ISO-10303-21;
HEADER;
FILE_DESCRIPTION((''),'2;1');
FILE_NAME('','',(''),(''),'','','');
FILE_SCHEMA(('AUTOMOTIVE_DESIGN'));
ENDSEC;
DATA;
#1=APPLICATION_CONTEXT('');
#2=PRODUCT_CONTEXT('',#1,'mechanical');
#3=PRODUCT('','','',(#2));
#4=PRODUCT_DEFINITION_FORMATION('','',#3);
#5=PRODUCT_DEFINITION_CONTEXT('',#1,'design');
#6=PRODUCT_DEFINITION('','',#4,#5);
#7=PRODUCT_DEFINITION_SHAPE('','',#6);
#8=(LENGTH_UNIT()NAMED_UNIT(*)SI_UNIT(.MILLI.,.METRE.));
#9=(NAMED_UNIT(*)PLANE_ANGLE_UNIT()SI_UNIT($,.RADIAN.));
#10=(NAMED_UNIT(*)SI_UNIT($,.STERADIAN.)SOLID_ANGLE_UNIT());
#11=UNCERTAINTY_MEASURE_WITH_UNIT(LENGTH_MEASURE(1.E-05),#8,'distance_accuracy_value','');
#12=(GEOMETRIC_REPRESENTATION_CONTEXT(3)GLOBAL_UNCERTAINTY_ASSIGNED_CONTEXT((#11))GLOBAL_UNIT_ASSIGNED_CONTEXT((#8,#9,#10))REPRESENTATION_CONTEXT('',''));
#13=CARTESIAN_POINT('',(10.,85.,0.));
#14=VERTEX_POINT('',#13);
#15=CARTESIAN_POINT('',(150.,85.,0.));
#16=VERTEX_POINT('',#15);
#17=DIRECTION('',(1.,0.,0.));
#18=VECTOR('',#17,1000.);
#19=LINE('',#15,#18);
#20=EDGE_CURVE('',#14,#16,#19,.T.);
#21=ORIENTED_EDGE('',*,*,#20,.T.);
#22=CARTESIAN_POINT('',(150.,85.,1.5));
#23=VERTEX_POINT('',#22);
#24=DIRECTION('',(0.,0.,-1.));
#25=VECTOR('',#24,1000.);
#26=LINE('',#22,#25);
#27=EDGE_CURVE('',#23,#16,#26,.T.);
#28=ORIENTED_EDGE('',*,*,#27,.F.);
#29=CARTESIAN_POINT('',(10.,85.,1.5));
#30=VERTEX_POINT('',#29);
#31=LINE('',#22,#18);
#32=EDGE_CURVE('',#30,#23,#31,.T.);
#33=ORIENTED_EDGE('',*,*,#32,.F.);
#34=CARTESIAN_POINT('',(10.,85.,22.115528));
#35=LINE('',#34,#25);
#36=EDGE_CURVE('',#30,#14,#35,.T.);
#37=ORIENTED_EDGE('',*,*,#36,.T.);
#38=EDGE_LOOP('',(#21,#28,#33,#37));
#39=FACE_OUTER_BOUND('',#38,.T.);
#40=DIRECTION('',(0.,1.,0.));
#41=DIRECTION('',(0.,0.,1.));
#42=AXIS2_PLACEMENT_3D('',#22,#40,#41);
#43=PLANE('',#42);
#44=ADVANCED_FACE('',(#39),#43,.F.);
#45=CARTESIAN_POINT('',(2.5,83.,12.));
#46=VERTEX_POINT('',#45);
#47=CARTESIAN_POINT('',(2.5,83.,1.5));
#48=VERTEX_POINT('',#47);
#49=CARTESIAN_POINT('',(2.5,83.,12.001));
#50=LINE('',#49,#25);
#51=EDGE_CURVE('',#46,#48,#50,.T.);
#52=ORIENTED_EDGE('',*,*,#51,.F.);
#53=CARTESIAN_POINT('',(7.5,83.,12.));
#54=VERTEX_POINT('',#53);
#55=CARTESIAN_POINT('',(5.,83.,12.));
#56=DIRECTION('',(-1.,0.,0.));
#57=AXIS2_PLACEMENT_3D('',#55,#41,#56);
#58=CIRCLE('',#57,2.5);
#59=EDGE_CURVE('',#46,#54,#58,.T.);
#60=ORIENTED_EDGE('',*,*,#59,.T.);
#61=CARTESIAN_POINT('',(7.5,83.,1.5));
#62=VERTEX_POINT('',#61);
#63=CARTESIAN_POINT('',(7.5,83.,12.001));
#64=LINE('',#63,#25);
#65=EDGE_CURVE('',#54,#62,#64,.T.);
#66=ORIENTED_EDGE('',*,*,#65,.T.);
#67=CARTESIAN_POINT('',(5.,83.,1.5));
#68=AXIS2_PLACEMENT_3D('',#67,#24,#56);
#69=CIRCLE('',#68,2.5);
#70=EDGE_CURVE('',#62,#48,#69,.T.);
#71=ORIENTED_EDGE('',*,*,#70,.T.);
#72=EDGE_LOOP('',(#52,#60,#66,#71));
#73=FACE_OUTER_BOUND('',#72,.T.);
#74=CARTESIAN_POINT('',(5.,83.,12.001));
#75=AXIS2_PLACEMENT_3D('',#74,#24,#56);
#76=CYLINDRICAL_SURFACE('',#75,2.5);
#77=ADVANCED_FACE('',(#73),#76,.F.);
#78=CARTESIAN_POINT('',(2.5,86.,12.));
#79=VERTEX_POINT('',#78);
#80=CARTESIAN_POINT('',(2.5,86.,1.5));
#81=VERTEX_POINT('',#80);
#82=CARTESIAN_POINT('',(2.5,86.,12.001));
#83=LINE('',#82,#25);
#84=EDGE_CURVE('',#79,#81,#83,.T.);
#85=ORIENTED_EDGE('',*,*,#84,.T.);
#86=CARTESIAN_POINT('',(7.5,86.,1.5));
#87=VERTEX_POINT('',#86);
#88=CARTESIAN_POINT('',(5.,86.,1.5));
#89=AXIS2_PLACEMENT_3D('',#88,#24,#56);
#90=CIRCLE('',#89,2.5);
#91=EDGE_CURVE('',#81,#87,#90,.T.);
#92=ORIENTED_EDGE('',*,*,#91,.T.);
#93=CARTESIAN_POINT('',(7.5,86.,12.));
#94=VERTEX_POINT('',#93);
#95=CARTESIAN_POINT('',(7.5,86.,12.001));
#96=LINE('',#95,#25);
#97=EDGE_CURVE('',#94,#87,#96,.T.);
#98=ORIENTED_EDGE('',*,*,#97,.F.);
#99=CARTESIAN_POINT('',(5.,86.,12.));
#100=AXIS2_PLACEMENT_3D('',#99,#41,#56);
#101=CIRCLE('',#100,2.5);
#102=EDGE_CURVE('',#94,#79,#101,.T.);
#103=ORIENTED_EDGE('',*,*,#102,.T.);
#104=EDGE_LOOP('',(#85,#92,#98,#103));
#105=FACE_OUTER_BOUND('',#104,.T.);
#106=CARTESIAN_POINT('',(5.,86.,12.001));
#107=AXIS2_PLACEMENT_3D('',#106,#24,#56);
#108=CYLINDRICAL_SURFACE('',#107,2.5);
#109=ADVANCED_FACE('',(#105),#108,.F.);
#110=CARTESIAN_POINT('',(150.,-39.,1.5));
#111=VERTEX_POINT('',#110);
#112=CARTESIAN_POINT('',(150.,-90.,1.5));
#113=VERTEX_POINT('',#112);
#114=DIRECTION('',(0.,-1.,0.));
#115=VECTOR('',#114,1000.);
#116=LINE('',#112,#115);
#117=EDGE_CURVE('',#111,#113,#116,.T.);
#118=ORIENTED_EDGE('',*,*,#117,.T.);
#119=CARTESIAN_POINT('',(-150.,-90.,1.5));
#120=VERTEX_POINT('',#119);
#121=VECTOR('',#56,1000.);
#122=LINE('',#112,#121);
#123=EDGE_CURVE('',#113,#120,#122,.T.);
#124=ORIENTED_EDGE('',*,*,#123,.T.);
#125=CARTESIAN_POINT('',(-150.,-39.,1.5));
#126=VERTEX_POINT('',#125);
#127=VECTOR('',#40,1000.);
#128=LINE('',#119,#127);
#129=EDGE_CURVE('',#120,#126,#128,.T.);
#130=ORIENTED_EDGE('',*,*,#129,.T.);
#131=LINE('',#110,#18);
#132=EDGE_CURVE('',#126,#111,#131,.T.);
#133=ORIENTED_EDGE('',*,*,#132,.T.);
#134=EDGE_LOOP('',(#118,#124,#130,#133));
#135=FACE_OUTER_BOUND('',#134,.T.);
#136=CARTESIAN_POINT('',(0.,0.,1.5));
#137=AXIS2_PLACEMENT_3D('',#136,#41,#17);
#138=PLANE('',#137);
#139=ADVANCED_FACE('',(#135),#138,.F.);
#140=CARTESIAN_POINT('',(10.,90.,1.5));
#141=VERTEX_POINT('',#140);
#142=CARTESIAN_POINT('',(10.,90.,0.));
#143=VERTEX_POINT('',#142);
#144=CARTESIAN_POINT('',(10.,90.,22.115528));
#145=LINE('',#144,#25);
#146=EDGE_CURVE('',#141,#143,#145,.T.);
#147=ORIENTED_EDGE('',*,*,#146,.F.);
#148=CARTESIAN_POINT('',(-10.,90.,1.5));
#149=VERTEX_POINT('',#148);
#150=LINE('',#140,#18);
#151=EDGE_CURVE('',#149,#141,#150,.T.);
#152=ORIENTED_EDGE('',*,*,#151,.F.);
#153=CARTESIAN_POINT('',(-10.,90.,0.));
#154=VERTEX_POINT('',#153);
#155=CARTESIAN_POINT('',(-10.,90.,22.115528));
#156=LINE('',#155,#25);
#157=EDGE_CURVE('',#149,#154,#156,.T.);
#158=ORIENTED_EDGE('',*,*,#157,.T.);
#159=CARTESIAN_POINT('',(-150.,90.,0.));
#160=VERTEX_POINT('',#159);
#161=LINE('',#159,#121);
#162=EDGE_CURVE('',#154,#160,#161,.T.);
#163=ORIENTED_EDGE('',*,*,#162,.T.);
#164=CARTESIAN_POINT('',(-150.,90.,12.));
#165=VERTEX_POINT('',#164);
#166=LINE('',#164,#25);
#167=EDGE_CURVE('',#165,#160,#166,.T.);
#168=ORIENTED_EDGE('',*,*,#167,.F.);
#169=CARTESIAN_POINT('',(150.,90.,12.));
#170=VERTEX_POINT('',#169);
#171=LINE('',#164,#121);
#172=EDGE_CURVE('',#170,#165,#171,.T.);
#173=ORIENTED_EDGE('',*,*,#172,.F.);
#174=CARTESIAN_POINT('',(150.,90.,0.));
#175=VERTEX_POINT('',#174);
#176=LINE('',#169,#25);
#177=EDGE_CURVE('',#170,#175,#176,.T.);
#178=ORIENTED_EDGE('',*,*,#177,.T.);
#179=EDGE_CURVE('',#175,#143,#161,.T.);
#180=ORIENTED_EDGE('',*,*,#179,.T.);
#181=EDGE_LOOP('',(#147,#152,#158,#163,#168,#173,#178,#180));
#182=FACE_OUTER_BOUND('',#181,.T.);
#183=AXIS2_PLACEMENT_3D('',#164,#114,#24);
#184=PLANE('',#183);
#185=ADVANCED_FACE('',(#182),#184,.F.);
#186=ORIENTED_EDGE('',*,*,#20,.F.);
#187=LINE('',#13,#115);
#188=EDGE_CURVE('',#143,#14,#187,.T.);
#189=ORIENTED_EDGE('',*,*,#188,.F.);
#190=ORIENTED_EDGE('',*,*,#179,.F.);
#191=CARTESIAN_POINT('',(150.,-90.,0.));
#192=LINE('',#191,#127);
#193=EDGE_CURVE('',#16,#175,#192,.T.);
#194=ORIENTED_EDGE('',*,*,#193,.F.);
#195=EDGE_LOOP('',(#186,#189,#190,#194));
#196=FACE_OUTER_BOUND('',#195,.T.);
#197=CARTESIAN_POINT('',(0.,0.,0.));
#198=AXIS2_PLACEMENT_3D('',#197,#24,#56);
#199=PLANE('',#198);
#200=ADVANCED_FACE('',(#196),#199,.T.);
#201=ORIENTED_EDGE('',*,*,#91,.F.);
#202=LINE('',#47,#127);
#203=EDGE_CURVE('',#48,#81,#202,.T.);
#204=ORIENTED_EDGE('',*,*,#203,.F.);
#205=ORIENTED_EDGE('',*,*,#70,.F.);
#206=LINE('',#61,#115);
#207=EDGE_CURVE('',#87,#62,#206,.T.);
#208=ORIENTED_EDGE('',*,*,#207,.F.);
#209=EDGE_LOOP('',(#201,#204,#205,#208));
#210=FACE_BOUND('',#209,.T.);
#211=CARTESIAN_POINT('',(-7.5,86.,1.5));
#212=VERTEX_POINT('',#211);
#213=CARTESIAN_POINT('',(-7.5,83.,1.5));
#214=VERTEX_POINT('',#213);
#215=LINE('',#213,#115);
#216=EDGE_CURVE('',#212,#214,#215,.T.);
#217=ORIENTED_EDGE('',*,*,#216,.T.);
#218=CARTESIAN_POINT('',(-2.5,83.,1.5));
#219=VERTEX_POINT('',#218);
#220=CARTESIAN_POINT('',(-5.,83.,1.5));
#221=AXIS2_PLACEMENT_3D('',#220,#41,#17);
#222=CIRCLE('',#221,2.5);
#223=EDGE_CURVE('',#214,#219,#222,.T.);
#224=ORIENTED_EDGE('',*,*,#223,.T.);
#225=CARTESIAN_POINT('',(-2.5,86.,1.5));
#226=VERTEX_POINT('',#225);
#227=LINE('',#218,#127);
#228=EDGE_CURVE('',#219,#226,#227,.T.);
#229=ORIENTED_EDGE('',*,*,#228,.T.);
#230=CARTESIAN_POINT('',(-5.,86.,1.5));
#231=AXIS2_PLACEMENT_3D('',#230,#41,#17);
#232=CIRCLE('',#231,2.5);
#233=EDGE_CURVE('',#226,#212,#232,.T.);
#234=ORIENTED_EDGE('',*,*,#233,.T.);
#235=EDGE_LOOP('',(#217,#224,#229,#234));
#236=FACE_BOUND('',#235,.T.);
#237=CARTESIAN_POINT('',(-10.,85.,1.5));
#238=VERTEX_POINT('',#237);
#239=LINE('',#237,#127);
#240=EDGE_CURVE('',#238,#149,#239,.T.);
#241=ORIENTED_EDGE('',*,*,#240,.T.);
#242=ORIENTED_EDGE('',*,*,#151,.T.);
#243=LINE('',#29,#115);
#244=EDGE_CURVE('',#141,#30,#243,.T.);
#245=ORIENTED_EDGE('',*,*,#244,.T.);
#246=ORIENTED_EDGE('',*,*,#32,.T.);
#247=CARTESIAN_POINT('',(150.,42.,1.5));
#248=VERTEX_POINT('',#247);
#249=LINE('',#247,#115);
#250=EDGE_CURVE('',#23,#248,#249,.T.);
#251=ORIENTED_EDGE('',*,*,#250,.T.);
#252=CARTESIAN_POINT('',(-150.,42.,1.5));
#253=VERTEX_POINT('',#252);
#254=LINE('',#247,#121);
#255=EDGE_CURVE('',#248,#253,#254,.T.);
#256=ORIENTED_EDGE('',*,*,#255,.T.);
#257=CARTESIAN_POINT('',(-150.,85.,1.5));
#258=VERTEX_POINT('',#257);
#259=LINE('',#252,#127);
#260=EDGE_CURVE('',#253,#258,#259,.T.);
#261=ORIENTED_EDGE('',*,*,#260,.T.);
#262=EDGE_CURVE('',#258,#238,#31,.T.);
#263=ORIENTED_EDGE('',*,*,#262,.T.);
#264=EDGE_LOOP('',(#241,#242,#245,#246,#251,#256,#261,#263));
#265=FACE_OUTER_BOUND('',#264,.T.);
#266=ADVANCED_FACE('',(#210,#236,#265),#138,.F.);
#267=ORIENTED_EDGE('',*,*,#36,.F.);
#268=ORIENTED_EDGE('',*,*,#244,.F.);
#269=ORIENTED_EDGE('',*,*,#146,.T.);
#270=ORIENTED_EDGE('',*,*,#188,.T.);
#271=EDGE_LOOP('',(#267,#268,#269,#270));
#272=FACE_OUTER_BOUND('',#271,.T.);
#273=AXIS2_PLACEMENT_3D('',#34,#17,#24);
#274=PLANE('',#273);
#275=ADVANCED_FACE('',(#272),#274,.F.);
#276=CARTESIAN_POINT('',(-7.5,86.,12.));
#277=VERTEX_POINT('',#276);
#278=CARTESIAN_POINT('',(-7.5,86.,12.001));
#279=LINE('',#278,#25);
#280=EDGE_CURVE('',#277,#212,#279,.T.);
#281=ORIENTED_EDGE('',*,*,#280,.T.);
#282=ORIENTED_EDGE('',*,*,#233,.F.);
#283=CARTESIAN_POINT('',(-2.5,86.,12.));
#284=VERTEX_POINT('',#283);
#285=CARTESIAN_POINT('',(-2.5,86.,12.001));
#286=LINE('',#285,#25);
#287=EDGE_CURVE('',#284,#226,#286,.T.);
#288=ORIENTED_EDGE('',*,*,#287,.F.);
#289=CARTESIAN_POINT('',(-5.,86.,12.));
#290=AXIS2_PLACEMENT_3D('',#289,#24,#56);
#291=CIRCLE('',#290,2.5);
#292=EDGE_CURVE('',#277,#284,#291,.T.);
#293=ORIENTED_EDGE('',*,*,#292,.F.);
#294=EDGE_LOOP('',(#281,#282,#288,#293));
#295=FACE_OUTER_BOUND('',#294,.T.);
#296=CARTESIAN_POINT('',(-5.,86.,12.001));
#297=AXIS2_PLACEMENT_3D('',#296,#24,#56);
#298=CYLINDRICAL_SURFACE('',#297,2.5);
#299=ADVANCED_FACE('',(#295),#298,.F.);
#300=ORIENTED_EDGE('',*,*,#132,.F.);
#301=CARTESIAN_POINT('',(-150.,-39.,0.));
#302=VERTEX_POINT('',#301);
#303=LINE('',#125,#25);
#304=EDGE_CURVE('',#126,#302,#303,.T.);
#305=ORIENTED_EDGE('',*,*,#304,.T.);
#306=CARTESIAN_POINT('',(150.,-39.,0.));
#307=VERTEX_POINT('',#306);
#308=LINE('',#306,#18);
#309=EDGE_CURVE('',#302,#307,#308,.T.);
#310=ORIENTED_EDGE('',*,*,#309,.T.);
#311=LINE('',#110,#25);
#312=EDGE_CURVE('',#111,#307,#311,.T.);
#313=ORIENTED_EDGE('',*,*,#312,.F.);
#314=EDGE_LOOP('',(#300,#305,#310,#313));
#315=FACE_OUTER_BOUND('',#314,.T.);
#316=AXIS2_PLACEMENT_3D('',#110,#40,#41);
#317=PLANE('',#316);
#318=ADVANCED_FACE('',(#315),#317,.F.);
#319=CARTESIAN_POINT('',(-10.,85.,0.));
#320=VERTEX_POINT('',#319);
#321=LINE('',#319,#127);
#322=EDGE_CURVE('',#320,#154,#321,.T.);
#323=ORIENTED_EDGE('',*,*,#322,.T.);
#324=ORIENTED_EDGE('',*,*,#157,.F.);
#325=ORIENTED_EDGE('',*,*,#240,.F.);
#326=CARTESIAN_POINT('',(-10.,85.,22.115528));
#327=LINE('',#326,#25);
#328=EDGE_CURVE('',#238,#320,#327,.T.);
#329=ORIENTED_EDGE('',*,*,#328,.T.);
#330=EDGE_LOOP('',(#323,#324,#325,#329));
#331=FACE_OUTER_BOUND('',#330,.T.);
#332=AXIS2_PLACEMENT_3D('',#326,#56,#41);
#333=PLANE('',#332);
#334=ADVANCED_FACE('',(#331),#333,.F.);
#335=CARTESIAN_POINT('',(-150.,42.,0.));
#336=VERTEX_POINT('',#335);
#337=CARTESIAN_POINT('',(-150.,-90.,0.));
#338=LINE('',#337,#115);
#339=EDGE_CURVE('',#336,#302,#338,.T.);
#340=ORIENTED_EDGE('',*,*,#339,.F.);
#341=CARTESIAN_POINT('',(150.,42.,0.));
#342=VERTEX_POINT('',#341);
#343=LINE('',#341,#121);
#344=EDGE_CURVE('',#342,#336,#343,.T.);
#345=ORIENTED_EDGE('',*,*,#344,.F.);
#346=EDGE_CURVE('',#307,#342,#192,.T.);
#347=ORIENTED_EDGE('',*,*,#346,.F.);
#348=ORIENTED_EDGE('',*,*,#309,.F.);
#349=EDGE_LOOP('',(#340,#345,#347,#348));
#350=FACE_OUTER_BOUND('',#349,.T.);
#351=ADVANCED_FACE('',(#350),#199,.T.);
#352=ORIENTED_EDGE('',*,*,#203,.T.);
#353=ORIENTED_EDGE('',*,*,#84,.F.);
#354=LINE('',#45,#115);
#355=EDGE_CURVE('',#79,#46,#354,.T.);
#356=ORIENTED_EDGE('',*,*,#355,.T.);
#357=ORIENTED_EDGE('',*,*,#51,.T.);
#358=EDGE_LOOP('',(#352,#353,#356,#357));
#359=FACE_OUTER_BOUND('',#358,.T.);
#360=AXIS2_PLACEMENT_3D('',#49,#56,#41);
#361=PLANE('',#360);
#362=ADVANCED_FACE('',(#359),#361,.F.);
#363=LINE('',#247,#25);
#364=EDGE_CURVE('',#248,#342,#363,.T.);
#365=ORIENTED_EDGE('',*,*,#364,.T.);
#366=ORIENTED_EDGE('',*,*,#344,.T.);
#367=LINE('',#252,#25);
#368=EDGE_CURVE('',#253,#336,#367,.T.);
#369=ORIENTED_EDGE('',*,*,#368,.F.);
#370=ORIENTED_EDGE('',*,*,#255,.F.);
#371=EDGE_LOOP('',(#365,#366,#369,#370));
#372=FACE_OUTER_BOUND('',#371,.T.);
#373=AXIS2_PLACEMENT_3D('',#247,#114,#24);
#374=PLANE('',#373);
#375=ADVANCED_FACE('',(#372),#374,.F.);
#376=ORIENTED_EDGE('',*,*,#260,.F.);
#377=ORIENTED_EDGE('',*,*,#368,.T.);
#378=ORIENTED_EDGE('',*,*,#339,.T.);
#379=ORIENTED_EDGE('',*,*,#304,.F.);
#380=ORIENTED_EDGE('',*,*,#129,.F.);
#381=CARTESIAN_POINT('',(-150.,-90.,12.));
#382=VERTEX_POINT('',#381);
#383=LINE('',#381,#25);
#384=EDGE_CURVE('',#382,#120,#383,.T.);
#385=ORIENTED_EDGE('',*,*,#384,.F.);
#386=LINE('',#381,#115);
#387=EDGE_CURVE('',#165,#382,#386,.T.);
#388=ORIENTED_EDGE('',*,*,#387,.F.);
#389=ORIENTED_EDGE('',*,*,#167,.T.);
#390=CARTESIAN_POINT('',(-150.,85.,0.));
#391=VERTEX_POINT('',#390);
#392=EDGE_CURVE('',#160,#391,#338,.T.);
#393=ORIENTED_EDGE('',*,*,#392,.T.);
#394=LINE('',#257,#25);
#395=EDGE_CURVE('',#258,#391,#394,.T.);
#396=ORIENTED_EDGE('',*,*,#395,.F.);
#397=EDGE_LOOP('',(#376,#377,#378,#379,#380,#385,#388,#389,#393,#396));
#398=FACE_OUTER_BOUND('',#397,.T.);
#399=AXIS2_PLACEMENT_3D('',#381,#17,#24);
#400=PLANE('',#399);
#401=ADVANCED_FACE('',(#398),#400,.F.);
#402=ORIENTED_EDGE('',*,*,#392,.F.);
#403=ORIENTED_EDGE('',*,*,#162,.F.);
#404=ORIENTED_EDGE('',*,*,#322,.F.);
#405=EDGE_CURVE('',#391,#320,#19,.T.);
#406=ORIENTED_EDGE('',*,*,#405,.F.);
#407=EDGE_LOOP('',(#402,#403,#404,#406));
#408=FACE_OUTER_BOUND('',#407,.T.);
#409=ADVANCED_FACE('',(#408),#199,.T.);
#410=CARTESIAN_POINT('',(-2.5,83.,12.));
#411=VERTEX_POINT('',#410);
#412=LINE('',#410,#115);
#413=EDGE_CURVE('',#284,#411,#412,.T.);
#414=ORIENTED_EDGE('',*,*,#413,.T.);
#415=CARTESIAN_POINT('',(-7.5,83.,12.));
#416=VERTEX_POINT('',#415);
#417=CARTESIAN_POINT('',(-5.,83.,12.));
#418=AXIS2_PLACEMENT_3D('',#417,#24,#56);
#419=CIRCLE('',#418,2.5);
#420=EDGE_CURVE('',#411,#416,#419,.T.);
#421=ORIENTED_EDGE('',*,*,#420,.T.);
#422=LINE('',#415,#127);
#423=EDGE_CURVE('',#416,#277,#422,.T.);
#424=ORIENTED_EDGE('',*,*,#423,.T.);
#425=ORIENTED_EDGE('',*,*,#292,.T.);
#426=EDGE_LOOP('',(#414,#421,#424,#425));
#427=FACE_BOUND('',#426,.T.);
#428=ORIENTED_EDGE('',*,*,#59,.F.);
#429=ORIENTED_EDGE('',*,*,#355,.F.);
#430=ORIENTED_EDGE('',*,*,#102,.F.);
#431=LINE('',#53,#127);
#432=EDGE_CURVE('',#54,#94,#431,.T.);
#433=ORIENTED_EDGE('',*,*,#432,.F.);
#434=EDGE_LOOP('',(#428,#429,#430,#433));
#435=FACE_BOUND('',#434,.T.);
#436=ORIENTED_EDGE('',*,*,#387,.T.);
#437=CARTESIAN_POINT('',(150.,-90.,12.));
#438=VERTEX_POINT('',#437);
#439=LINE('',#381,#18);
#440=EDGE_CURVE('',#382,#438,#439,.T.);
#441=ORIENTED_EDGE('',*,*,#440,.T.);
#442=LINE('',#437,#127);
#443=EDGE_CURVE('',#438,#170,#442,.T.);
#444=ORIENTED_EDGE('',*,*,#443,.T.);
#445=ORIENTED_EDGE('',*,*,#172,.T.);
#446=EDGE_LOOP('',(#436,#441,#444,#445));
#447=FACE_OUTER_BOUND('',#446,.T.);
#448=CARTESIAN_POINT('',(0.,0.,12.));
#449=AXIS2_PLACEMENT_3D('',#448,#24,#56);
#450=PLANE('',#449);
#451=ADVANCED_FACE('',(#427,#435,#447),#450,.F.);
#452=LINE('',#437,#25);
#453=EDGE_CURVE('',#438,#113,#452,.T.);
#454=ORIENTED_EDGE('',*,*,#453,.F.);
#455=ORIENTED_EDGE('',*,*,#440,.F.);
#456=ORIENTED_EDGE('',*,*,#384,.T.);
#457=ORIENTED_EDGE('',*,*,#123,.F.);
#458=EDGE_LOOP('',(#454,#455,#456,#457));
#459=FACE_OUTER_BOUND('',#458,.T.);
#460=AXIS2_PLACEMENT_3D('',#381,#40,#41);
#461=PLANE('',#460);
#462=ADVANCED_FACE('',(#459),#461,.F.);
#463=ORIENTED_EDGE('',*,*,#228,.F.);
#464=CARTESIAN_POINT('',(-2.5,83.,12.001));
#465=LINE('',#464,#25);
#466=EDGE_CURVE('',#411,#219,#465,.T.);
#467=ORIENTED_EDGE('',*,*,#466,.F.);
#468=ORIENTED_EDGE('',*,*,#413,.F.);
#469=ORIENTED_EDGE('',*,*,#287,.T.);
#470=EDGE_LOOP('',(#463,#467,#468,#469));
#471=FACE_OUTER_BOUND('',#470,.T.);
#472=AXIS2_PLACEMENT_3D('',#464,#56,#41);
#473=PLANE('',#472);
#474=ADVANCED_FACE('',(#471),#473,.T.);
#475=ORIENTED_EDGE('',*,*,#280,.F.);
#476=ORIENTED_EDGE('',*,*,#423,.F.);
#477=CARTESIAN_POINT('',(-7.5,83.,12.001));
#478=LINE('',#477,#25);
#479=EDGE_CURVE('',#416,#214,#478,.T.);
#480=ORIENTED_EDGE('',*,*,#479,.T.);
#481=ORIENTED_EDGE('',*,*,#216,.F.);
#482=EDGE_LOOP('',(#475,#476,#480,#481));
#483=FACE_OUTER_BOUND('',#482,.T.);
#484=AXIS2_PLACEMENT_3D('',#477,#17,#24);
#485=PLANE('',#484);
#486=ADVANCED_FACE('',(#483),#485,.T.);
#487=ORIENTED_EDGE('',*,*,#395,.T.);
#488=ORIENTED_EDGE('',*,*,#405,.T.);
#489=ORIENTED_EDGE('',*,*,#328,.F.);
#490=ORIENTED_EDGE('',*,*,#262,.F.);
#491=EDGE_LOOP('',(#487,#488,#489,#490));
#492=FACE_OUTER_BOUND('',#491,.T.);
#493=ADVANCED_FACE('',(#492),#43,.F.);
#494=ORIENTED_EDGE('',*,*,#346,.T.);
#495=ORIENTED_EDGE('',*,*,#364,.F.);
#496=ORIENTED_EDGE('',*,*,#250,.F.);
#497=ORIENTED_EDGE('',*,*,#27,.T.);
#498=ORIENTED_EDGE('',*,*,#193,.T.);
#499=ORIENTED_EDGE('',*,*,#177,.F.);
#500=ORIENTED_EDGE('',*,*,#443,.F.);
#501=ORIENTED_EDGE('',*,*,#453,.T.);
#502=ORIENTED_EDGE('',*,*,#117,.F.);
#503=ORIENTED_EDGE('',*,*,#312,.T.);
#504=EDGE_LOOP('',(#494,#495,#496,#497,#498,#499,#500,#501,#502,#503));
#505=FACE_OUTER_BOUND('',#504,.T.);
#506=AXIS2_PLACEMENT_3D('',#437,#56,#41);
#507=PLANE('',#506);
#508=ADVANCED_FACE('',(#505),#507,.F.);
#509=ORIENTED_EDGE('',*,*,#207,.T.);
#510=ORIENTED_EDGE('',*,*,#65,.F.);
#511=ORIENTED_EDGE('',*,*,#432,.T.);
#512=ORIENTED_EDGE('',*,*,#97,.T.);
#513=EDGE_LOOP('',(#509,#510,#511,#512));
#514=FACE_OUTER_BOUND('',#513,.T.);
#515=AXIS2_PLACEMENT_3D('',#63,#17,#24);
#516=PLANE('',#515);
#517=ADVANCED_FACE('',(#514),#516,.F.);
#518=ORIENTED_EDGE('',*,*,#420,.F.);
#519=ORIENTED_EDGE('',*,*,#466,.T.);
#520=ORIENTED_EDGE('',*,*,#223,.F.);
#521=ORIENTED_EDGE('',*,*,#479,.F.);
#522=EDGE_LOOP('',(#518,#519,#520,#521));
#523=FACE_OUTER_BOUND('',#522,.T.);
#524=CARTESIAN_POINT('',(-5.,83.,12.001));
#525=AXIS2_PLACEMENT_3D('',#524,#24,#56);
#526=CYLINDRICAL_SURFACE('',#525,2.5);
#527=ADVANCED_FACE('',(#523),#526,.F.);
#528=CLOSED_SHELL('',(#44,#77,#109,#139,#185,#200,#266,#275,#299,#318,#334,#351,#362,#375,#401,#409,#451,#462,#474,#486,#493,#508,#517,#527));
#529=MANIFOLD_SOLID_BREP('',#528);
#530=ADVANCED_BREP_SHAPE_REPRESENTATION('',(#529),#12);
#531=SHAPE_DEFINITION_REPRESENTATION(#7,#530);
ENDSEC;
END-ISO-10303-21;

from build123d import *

# Parameters (mm, degrees)
SKETCH_1_W          = 300
SKETCH_1_H          = 180
EXTRUDE_1_DEPTH     = 12
SKETCH_2_W          = 300
SKETCH_2_H          = 43
SKETCH_2_H_2        = 51
CUT_EXTRUDE_1_DEPTH = 1.5
SKETCH_3_W          = 20
SKETCH_3_H          = 5
CUT_EXTRUDE_2_DEPTH = 1.5
CUT_EXTRUDE_3_REACH = 177.243


with BuildPart() as part:
    # 草图1 → 凸台-拉伸1 (new body)
    with BuildSketch(Plane.XY):
        Rectangle(SKETCH_1_W, SKETCH_1_H)
    extrude(amount=EXTRUDE_1_DEPTH)

    # 草图2 → 切除-拉伸1 (cut)
    with BuildSketch(Plane(origin=(0, 0, 0), x_dir=(-1, 0, 0), z_dir=(0, 0, -1))):
        with Locations((0, 63.5)):
            Rectangle(SKETCH_2_W, SKETCH_2_H)
        with Locations((0, -64.5)):
            Rectangle(SKETCH_2_W, SKETCH_2_H_2)
    extrude(amount=-CUT_EXTRUDE_1_DEPTH, mode=Mode.SUBTRACT)

    # 草图3 → 切除-拉伸2 (cut)
    with BuildSketch(Plane(origin=(0, 0, 0), x_dir=(-1, 0, 0), z_dir=(0, 0, -1))):
        with Locations((0, 87.5)):
            Rectangle(SKETCH_3_W, SKETCH_3_H)
    extrude(amount=-CUT_EXTRUDE_2_DEPTH, mode=Mode.SUBTRACT)

    # 草图4 → 切除-拉伸3 (cut, up to next)
    with BuildSketch(Plane(origin=(0, 0, 1.5), x_dir=(-1, 0, 0), z_dir=(0, 0, -1)), mode=Mode.PRIVATE) as cut_extrude_3_sk1:
        with BuildLine():
            Line((-7.5, 83), (-7.5, 86))
            ThreePointArc((-7.5, 86), (-5, 88.5), (-2.5, 86))
            Line((-2.5, 86), (-2.5, 83))
            ThreePointArc((-2.5, 83), (-5, 80.5), (-7.5, 83))
        make_face()
    cut_extrude_3_tool1 = extrude(cut_extrude_3_sk1.sketch, amount=-CUT_EXTRUDE_3_REACH, mode=Mode.PRIVATE) & part.part
    cut_extrude_3 = cut_extrude_3_tool1.solids().sort_by_distance((5, 84.5, 1.5))[0]
    add(cut_extrude_3, mode=Mode.SUBTRACT)

    # 镜向1: 切除-拉伸3 across plane
    add(cut_extrude_3.mirror(Plane(origin=(0, 0, 0), x_dir=(0, 0, 1), z_dir=(1, 0, 0))), mode=Mode.SUBTRACT)


solid = part.part
